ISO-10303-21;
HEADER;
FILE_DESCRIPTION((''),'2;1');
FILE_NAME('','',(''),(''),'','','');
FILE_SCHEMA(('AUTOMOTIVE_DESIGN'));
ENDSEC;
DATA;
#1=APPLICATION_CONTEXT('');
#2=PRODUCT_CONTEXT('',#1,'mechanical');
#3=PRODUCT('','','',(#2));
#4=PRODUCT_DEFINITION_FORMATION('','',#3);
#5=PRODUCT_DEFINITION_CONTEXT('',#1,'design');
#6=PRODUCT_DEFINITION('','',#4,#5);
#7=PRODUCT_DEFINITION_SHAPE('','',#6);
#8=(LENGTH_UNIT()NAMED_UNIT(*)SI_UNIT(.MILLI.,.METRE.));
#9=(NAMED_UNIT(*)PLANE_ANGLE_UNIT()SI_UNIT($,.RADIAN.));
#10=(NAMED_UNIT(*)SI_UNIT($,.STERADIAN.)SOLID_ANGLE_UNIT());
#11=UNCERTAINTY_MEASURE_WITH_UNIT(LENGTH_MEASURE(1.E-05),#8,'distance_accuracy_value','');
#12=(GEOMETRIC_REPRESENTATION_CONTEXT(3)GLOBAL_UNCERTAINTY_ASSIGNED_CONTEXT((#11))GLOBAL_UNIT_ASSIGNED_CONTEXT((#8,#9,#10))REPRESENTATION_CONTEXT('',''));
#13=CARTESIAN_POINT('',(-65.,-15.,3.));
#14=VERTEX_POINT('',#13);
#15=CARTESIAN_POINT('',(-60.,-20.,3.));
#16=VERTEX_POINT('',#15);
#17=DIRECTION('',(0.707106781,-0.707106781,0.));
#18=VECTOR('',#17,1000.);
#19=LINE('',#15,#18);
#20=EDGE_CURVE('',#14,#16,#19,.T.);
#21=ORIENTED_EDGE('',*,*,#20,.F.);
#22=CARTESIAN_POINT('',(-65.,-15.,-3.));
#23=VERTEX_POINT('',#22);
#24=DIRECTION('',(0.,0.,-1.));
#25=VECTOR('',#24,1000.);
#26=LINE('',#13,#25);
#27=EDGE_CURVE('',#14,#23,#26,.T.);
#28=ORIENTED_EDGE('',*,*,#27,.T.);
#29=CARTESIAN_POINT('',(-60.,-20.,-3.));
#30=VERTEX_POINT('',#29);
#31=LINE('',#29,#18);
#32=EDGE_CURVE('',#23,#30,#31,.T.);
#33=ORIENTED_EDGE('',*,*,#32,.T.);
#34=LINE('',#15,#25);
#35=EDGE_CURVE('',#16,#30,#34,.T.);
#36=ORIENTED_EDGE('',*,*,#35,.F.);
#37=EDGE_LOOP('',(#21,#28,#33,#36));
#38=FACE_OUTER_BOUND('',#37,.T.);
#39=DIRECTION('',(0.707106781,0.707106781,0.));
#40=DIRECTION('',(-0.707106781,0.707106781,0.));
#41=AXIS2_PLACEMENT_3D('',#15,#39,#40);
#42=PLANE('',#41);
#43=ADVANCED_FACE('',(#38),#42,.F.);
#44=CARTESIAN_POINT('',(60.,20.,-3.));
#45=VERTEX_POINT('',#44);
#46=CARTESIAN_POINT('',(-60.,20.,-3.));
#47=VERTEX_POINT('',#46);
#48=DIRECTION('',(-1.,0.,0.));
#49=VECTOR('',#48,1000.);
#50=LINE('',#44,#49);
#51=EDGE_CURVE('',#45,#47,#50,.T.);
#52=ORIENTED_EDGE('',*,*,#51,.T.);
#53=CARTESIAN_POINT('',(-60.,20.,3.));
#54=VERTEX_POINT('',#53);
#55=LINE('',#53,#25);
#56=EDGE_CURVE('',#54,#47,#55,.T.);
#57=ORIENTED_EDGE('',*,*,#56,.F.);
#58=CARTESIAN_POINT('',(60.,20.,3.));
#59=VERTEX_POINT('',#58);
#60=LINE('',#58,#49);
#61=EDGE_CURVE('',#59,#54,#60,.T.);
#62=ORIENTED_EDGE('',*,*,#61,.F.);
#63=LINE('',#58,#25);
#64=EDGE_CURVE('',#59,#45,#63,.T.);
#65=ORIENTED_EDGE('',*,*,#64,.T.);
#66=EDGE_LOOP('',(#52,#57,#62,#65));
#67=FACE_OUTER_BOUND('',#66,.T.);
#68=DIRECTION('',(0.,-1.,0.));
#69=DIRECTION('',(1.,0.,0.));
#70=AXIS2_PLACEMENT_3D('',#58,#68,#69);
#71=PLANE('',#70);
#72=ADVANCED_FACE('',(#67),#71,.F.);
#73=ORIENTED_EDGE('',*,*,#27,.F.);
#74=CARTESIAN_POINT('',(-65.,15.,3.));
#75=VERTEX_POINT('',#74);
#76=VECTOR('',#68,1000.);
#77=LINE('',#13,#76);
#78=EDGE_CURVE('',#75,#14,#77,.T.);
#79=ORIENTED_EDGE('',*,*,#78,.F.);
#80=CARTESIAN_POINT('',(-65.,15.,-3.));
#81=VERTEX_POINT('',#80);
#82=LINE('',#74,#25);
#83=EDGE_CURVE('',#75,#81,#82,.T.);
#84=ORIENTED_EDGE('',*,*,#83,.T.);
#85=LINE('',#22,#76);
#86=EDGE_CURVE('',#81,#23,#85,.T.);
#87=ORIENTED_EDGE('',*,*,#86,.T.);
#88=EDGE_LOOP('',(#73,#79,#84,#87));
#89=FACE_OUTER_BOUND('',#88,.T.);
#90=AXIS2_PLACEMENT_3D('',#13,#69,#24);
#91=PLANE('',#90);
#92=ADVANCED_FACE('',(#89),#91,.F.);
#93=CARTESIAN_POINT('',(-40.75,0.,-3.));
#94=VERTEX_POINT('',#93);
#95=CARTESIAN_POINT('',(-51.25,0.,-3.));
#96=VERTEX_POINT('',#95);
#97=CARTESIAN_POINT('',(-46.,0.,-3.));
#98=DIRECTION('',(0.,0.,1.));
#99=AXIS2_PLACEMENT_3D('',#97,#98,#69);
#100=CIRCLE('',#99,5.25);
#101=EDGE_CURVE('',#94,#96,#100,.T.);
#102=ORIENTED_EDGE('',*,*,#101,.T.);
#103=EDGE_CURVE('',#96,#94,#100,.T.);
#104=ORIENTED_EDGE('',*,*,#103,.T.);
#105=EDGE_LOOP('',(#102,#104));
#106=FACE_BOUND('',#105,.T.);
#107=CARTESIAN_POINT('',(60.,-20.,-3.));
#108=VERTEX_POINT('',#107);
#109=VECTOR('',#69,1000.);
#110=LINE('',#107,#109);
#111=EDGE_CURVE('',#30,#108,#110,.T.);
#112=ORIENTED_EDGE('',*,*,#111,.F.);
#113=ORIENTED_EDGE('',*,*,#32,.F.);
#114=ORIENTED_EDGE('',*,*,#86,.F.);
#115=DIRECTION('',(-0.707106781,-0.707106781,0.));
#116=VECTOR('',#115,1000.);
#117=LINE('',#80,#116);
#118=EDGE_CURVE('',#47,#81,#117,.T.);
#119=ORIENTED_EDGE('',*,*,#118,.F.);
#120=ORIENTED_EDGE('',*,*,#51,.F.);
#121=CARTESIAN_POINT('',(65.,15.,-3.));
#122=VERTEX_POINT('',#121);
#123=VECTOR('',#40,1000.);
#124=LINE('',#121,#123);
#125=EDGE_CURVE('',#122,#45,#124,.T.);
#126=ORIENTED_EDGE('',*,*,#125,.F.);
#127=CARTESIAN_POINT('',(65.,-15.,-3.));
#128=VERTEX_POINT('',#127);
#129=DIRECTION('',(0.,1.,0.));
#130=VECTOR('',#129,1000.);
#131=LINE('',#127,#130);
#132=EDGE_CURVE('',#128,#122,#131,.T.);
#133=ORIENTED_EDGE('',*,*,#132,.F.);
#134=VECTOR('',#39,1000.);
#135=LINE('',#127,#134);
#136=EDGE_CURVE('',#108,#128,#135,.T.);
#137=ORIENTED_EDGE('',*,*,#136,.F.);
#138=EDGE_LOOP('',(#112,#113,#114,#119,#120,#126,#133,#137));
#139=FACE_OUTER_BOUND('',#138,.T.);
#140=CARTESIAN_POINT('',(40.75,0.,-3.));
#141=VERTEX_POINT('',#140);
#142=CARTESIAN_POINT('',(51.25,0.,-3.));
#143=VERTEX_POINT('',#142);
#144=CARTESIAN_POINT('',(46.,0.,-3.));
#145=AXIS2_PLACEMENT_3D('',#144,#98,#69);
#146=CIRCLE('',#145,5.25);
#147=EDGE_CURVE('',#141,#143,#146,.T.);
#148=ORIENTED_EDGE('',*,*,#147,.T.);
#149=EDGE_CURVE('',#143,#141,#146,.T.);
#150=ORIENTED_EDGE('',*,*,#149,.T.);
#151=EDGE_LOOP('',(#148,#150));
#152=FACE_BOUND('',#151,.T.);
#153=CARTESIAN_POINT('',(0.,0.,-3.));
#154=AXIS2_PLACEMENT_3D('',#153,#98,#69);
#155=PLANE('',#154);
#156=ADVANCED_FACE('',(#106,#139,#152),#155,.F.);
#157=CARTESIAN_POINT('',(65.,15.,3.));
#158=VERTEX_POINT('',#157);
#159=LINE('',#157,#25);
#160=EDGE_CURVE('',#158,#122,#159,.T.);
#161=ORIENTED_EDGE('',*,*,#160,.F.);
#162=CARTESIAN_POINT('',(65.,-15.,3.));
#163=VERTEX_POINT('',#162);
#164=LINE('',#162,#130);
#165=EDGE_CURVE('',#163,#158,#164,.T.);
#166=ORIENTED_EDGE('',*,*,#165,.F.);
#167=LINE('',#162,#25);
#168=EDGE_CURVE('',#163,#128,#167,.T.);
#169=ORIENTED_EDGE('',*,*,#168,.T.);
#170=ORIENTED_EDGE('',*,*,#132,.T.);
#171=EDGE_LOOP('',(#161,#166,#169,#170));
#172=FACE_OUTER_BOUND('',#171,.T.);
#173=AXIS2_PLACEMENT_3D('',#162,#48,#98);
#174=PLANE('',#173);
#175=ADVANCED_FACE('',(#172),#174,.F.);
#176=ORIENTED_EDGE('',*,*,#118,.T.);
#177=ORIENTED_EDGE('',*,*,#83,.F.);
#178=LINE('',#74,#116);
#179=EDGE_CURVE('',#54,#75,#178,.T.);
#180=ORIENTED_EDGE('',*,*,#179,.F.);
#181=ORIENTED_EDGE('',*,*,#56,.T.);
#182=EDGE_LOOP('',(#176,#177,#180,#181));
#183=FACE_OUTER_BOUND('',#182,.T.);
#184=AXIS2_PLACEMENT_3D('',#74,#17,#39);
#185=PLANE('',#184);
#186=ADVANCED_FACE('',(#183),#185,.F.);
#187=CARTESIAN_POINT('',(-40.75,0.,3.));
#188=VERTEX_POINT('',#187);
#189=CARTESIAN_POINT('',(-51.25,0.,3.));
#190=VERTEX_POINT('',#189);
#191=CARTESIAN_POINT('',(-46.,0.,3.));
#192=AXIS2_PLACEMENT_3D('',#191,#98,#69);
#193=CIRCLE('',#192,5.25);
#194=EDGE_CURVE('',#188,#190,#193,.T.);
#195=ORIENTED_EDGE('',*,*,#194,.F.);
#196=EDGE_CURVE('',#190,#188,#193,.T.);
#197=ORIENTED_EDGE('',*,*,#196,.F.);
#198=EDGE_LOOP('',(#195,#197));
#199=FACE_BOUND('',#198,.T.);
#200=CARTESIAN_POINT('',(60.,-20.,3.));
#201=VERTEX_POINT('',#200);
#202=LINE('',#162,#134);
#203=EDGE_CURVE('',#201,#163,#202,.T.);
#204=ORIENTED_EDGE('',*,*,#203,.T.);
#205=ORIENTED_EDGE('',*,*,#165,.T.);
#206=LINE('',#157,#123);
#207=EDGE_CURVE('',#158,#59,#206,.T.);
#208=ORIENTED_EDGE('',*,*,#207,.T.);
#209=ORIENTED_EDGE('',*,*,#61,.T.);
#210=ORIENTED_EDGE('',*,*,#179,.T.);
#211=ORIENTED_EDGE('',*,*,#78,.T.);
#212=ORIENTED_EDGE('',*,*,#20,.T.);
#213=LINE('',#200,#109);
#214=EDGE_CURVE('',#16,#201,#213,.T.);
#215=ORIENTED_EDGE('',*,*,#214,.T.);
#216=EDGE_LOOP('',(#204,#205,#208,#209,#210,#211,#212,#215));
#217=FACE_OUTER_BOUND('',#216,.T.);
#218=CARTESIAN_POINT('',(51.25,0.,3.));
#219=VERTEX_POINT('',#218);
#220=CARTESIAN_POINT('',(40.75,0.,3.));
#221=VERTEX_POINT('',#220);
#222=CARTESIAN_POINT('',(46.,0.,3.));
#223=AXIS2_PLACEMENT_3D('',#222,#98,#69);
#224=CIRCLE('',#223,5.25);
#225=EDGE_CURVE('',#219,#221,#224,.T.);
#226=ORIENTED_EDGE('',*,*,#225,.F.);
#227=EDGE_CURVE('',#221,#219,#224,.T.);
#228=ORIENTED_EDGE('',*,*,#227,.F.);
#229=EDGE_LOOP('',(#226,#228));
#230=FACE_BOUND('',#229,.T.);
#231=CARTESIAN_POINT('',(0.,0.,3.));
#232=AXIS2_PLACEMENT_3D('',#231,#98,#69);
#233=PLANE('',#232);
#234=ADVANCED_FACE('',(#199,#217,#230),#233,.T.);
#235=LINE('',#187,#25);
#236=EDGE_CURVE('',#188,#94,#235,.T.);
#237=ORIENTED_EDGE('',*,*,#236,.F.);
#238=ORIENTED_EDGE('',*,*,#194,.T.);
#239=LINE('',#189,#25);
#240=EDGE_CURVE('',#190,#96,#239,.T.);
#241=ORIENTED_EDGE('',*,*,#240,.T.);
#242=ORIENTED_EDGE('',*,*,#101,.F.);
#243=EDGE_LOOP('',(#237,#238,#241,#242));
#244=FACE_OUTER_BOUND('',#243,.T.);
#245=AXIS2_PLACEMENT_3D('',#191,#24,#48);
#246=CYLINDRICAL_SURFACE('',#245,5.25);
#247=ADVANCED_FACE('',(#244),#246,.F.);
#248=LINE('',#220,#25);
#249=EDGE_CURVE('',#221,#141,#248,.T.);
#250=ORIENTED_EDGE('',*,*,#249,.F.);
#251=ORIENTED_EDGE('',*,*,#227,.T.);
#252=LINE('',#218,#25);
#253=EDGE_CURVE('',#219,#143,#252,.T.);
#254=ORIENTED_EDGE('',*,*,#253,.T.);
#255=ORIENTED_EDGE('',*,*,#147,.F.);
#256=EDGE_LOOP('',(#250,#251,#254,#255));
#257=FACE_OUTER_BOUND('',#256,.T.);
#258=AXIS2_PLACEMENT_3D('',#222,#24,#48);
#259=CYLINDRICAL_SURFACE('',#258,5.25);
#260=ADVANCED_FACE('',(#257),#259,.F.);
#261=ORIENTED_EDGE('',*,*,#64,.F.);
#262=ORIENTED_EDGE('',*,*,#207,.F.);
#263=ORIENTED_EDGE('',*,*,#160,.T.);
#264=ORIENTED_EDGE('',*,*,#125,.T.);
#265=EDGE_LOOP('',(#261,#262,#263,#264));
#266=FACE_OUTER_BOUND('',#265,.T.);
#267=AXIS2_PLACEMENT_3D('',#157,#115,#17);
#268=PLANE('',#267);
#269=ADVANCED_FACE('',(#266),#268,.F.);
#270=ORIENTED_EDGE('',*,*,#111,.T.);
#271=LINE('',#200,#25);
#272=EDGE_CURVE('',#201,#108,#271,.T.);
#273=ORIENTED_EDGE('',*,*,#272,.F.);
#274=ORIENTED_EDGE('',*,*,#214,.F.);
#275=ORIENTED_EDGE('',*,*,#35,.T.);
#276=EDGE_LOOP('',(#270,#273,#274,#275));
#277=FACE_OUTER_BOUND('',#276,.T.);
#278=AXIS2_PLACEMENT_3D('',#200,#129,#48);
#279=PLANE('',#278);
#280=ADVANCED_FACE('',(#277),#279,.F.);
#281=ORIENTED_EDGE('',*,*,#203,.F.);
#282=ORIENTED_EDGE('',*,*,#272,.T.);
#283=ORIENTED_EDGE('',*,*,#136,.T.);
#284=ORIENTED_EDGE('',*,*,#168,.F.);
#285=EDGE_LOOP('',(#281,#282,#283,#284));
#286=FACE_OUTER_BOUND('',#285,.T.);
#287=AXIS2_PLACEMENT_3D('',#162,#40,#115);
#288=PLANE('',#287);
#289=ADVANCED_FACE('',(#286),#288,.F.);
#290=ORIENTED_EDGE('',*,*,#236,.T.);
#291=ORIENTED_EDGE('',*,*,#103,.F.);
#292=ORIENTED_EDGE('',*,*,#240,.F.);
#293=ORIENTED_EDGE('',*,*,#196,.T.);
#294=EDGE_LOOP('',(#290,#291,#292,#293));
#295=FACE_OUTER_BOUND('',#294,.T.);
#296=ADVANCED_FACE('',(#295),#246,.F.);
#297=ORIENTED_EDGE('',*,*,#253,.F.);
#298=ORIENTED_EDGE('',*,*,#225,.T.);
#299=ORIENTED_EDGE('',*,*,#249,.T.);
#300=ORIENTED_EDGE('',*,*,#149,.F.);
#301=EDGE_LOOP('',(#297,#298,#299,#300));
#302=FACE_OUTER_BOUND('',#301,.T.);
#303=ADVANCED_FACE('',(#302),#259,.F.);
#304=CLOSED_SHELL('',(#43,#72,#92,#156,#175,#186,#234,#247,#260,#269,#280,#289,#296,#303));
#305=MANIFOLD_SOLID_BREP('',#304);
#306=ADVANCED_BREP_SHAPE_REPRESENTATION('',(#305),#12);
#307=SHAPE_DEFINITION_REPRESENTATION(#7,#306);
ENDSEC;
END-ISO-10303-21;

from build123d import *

# Parameters (mm, degrees)
SKETCH1_R           = 5.25
BOSS_EXTRUDE1_DEPTH = 3


with BuildPart() as part:
    # Sketch1 → Boss-Extrude1 (new, symmetric)
    with BuildSketch(Plane.XY):
        Polygon((-65, 15), (-60, 20), (60, 20), (65, 15), (65, -15), (60, -20), (-60, -20), (-65, -15), align=None)
        with Locations((-46, 0)):
            Circle(SKETCH1_R, mode=Mode.SUBTRACT)
        with Locations((46, 0)):
            Circle(SKETCH1_R, mode=Mode.SUBTRACT)
    extrude(amount=BOSS_EXTRUDE1_DEPTH, both=True)


solid = part.part
